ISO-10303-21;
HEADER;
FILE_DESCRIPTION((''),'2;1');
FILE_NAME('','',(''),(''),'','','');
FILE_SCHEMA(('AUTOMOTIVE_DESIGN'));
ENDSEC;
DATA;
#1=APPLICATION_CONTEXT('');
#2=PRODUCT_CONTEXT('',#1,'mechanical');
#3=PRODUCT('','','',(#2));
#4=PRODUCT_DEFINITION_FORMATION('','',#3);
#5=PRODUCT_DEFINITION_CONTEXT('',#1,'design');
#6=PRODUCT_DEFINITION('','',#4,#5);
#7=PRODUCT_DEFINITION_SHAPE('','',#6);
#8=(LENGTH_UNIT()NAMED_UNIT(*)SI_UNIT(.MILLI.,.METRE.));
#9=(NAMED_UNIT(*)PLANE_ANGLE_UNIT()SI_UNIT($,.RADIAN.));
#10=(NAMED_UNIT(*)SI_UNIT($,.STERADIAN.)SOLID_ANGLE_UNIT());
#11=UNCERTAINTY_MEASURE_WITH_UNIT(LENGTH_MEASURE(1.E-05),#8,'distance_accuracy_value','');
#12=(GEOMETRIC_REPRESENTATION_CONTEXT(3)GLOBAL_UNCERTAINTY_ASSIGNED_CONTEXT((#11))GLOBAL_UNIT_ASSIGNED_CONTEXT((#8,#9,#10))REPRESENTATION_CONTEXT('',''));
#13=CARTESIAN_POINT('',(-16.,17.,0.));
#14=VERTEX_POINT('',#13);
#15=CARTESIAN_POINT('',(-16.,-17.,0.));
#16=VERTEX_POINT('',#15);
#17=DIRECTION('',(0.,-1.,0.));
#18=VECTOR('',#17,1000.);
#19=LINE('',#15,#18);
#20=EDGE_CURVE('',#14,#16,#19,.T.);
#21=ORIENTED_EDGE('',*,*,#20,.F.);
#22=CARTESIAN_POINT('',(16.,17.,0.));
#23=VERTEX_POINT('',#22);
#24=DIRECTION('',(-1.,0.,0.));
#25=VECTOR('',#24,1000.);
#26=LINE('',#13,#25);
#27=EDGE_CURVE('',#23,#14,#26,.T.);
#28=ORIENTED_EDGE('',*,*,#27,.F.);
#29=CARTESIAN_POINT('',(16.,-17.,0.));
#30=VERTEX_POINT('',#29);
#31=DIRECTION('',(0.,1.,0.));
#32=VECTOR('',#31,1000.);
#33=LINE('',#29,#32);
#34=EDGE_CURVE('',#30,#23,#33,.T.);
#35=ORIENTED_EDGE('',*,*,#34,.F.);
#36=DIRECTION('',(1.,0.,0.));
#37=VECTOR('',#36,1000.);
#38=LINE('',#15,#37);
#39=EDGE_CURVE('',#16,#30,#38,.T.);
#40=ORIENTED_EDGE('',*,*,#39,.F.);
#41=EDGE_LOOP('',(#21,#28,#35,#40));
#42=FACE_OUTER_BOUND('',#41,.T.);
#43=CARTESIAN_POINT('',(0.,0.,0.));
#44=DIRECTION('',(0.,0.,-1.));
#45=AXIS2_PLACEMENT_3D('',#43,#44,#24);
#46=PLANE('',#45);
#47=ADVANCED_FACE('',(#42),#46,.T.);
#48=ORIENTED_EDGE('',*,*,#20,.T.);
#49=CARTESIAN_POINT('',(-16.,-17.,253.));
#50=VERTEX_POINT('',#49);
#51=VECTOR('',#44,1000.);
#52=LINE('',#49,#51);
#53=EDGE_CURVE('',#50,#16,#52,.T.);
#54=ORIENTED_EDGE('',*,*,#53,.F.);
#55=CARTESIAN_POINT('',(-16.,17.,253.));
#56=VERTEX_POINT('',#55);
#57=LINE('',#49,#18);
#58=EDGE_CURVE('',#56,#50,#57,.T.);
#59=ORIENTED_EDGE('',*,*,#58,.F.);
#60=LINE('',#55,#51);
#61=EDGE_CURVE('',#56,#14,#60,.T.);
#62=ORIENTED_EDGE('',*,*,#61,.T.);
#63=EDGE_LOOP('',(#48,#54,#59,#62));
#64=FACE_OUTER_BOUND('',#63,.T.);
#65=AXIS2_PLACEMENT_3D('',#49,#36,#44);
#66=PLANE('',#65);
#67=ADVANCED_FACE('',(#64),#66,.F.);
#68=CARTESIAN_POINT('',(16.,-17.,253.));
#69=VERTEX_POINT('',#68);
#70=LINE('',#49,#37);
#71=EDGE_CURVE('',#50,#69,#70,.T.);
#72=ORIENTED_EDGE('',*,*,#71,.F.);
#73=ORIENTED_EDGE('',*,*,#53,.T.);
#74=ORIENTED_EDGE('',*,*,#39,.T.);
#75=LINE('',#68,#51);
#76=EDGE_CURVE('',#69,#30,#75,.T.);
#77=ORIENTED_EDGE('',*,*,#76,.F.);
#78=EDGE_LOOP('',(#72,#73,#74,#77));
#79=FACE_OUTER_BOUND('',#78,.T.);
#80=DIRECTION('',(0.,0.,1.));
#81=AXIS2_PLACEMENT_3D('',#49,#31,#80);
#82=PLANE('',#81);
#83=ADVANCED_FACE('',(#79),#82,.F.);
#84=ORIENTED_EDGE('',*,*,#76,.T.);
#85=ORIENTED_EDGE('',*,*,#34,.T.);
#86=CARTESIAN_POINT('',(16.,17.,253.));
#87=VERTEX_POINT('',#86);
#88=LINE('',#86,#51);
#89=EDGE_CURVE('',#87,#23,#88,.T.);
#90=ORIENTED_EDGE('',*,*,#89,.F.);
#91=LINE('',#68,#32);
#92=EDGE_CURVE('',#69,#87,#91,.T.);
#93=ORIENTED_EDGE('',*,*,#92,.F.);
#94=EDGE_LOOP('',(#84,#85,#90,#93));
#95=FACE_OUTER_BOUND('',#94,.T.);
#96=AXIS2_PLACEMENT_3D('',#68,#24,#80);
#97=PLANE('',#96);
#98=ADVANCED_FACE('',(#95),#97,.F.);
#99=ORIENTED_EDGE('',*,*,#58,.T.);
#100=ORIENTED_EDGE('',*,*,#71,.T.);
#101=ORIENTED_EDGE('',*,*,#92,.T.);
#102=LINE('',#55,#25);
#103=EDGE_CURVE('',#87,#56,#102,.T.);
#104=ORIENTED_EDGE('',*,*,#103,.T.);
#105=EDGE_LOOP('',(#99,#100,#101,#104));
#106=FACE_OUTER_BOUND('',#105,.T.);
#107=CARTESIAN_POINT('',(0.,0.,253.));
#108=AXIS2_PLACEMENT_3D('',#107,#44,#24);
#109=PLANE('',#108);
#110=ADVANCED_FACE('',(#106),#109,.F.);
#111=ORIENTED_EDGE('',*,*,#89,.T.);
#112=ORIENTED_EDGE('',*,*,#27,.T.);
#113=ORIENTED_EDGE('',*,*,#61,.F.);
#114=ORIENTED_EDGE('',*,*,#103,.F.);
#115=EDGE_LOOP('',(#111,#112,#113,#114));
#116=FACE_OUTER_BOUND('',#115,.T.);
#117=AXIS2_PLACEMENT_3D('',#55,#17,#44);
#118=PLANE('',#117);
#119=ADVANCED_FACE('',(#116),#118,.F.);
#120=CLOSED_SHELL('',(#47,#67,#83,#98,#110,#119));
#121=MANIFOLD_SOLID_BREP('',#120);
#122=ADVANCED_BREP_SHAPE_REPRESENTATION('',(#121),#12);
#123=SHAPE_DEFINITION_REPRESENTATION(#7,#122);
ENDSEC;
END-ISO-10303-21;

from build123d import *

# Parameters (mm, degrees)
SKETCH_1_W      = 32
SKETCH_1_H      = 34
EXTRUDE_1_DEPTH = 253


with BuildPart() as part:
    # 草图1 → 凸台-拉伸1 (new body)
    with BuildSketch(Plane.XY):
        Rectangle(SKETCH_1_W, SKETCH_1_H)
    extrude(amount=EXTRUDE_1_DEPTH)


solid = part.part
